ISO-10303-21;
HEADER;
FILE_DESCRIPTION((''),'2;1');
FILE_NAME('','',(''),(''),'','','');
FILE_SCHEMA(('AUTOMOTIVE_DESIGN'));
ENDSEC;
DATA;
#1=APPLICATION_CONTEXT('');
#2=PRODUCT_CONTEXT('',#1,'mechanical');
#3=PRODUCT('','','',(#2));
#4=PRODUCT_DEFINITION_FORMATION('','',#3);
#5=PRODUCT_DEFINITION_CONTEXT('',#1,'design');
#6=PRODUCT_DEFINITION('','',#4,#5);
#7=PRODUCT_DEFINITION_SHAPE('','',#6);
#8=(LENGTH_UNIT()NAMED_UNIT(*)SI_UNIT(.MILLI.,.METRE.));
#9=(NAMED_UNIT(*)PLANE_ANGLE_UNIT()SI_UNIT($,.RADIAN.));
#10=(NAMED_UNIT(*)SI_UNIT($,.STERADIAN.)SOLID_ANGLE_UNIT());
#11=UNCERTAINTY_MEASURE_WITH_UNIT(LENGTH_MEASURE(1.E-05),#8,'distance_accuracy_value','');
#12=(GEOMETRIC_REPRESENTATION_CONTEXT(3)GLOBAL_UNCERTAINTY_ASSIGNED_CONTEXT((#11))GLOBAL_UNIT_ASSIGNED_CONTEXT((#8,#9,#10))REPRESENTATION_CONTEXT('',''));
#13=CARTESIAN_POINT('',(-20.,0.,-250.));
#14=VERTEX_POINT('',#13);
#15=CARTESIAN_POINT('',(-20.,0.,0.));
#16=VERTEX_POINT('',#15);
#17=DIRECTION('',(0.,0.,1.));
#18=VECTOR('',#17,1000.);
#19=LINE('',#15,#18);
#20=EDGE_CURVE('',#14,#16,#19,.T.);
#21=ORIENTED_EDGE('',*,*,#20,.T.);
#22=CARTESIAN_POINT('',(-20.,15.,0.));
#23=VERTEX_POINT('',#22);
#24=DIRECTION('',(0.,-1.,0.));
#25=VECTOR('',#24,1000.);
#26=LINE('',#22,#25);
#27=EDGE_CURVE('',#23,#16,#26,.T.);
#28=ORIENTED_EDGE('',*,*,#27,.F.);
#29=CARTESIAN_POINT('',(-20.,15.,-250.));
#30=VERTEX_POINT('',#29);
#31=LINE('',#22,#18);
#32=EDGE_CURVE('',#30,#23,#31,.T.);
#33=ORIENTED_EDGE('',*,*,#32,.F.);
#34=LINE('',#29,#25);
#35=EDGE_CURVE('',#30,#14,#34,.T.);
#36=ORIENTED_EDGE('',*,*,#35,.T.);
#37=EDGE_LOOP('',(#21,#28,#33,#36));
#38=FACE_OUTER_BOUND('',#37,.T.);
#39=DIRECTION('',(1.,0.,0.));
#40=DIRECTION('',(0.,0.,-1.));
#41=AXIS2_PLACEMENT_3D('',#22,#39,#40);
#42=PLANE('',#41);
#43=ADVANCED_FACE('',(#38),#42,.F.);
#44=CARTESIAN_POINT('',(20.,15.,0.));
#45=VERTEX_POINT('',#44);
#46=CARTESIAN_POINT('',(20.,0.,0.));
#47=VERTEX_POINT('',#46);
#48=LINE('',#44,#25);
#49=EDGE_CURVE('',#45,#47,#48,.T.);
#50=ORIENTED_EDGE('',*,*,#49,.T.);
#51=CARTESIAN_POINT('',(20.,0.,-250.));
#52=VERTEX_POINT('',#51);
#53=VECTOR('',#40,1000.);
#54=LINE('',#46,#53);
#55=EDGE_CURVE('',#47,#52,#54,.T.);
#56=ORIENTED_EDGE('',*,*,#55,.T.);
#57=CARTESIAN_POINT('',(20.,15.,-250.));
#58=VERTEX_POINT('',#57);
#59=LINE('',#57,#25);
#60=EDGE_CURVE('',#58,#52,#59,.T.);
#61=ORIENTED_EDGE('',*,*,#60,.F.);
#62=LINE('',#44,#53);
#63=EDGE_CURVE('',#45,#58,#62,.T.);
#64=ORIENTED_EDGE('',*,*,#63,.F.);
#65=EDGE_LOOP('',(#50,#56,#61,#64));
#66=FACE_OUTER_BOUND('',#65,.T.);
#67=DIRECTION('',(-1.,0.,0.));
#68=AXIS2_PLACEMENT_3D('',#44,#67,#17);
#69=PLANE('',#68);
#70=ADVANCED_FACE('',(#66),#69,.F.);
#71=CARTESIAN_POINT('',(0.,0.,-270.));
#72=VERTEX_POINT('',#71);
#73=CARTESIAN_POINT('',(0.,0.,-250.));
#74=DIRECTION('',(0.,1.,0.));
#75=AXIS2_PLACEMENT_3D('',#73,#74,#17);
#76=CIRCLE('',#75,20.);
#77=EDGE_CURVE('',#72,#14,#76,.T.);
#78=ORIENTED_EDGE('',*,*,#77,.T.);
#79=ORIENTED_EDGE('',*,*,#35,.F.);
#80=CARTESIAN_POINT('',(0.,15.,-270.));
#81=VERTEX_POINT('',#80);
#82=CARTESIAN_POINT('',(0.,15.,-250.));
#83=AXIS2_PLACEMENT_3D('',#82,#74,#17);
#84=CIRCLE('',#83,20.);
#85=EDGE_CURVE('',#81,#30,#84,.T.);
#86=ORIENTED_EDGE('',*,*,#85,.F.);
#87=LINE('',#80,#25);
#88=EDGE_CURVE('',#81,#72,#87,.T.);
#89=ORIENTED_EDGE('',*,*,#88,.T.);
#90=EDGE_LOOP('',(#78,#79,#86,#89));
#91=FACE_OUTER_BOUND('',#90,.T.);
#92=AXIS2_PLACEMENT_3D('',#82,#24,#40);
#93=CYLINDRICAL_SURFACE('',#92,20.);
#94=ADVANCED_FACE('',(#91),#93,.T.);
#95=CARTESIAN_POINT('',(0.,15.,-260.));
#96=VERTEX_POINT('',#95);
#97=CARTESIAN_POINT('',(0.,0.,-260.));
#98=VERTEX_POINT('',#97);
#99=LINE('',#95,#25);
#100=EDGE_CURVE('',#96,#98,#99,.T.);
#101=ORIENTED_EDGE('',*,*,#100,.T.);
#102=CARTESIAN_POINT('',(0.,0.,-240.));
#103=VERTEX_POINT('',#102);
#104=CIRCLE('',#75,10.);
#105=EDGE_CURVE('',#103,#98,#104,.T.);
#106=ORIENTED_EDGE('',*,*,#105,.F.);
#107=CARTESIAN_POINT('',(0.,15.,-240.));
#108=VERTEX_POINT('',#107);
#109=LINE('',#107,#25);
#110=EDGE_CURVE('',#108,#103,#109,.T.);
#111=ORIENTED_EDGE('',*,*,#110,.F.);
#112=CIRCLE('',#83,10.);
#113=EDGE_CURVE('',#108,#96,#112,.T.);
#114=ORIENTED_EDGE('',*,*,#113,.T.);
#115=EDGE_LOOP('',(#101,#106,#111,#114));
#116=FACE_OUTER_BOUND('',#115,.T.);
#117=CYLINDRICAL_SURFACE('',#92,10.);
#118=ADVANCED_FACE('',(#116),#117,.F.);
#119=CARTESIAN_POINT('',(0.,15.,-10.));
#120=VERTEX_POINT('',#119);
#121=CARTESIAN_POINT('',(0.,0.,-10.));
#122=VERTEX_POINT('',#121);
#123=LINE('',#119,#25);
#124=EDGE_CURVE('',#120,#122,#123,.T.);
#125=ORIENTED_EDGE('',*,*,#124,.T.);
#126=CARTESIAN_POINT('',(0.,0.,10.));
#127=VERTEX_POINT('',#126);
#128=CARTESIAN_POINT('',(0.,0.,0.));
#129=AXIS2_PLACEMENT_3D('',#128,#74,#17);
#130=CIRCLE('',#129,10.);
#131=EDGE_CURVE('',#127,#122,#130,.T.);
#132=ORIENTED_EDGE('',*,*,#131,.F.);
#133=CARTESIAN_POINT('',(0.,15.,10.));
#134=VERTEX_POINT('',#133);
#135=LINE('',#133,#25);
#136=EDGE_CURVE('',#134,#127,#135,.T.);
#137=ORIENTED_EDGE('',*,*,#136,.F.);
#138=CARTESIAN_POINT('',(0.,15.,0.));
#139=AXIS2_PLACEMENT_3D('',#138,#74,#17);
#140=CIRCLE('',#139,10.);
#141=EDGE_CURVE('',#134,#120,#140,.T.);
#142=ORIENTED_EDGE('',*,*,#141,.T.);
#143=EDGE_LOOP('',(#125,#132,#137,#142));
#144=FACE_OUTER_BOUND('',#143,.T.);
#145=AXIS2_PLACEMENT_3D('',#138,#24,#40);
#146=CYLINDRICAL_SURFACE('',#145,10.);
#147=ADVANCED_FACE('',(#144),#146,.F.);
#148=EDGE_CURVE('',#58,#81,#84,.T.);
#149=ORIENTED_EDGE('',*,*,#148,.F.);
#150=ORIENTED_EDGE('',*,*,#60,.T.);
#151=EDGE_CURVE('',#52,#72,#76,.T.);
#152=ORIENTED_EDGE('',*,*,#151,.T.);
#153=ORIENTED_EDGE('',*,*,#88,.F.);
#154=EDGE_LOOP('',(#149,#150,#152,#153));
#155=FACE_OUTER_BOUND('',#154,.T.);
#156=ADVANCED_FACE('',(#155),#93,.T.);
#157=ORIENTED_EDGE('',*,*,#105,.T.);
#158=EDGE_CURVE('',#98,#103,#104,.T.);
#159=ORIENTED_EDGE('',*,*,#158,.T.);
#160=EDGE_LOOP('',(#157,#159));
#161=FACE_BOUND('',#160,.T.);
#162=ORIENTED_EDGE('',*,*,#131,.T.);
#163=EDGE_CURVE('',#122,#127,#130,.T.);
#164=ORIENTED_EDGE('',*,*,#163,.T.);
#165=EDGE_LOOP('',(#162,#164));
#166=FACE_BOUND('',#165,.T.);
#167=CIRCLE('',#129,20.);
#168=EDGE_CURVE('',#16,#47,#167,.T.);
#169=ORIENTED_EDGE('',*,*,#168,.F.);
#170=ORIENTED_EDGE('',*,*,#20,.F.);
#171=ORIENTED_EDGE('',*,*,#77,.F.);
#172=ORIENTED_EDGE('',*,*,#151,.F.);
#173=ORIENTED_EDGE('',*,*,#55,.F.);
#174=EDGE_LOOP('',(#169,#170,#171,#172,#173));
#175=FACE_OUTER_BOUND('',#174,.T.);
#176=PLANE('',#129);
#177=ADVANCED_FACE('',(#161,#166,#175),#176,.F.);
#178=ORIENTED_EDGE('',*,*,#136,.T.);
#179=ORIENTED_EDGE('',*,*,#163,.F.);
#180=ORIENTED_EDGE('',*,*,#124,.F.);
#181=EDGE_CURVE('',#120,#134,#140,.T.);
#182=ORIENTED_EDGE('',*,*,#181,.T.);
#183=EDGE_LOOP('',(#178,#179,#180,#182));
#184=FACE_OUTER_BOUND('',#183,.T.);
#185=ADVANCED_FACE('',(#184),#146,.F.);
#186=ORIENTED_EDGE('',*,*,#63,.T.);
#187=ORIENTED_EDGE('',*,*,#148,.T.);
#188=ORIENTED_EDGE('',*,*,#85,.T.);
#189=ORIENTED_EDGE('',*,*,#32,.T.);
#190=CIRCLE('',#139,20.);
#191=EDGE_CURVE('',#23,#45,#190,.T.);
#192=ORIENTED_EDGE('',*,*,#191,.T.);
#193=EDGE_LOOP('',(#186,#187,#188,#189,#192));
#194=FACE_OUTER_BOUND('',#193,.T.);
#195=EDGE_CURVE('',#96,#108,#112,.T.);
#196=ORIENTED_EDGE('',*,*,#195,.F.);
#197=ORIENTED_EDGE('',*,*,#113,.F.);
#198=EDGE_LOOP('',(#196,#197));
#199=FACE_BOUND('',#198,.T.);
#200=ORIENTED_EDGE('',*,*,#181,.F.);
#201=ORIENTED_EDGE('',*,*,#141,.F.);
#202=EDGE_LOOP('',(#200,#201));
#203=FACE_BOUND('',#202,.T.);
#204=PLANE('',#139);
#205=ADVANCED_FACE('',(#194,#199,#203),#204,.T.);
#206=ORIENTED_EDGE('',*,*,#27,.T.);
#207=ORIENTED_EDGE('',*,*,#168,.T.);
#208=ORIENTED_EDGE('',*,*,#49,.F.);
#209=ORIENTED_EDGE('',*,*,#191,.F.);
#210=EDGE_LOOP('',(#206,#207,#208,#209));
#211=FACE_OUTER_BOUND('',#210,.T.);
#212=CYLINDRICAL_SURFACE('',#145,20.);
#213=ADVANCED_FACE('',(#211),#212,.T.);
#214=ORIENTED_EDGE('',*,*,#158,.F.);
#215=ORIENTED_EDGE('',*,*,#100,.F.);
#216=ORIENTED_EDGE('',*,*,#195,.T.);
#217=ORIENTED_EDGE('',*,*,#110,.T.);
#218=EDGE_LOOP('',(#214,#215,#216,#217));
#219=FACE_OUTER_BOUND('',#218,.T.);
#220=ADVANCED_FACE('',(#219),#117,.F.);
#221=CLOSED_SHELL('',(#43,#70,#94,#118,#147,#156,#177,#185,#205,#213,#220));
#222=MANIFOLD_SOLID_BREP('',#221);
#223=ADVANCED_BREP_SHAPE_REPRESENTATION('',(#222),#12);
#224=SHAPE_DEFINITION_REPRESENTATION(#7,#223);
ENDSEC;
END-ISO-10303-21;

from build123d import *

# Parameters (mm, degrees)
SKETCH1_R           = 10
BOSS_EXTRUDE1_DEPTH = 15


with BuildPart() as part:
    # Sketch1 → Boss-Extrude1 (new body)
    with BuildSketch(Plane(origin=(0, 0, 0), x_dir=(1, 0, 0), z_dir=(0, 1, 0))):
        with BuildLine():
            Line((-20, 0), (-20, 250))
            ThreePointArc((-20, 250), (0, 270), (20, 250))
            Line((20, 250), (20, 0))
            ThreePointArc((20, 0), (0, -20), (-20, 0))
        make_face()
        with Locations(Location((0, 250, 0), (0, 0, 270))):
            Circle(SKETCH1_R, mode=Mode.SUBTRACT)
        with Locations(Location((0, 0, 0), (0, 0, 270))):
            Circle(SKETCH1_R, mode=Mode.SUBTRACT)
    extrude(amount=BOSS_EXTRUDE1_DEPTH)


solid = part.part
